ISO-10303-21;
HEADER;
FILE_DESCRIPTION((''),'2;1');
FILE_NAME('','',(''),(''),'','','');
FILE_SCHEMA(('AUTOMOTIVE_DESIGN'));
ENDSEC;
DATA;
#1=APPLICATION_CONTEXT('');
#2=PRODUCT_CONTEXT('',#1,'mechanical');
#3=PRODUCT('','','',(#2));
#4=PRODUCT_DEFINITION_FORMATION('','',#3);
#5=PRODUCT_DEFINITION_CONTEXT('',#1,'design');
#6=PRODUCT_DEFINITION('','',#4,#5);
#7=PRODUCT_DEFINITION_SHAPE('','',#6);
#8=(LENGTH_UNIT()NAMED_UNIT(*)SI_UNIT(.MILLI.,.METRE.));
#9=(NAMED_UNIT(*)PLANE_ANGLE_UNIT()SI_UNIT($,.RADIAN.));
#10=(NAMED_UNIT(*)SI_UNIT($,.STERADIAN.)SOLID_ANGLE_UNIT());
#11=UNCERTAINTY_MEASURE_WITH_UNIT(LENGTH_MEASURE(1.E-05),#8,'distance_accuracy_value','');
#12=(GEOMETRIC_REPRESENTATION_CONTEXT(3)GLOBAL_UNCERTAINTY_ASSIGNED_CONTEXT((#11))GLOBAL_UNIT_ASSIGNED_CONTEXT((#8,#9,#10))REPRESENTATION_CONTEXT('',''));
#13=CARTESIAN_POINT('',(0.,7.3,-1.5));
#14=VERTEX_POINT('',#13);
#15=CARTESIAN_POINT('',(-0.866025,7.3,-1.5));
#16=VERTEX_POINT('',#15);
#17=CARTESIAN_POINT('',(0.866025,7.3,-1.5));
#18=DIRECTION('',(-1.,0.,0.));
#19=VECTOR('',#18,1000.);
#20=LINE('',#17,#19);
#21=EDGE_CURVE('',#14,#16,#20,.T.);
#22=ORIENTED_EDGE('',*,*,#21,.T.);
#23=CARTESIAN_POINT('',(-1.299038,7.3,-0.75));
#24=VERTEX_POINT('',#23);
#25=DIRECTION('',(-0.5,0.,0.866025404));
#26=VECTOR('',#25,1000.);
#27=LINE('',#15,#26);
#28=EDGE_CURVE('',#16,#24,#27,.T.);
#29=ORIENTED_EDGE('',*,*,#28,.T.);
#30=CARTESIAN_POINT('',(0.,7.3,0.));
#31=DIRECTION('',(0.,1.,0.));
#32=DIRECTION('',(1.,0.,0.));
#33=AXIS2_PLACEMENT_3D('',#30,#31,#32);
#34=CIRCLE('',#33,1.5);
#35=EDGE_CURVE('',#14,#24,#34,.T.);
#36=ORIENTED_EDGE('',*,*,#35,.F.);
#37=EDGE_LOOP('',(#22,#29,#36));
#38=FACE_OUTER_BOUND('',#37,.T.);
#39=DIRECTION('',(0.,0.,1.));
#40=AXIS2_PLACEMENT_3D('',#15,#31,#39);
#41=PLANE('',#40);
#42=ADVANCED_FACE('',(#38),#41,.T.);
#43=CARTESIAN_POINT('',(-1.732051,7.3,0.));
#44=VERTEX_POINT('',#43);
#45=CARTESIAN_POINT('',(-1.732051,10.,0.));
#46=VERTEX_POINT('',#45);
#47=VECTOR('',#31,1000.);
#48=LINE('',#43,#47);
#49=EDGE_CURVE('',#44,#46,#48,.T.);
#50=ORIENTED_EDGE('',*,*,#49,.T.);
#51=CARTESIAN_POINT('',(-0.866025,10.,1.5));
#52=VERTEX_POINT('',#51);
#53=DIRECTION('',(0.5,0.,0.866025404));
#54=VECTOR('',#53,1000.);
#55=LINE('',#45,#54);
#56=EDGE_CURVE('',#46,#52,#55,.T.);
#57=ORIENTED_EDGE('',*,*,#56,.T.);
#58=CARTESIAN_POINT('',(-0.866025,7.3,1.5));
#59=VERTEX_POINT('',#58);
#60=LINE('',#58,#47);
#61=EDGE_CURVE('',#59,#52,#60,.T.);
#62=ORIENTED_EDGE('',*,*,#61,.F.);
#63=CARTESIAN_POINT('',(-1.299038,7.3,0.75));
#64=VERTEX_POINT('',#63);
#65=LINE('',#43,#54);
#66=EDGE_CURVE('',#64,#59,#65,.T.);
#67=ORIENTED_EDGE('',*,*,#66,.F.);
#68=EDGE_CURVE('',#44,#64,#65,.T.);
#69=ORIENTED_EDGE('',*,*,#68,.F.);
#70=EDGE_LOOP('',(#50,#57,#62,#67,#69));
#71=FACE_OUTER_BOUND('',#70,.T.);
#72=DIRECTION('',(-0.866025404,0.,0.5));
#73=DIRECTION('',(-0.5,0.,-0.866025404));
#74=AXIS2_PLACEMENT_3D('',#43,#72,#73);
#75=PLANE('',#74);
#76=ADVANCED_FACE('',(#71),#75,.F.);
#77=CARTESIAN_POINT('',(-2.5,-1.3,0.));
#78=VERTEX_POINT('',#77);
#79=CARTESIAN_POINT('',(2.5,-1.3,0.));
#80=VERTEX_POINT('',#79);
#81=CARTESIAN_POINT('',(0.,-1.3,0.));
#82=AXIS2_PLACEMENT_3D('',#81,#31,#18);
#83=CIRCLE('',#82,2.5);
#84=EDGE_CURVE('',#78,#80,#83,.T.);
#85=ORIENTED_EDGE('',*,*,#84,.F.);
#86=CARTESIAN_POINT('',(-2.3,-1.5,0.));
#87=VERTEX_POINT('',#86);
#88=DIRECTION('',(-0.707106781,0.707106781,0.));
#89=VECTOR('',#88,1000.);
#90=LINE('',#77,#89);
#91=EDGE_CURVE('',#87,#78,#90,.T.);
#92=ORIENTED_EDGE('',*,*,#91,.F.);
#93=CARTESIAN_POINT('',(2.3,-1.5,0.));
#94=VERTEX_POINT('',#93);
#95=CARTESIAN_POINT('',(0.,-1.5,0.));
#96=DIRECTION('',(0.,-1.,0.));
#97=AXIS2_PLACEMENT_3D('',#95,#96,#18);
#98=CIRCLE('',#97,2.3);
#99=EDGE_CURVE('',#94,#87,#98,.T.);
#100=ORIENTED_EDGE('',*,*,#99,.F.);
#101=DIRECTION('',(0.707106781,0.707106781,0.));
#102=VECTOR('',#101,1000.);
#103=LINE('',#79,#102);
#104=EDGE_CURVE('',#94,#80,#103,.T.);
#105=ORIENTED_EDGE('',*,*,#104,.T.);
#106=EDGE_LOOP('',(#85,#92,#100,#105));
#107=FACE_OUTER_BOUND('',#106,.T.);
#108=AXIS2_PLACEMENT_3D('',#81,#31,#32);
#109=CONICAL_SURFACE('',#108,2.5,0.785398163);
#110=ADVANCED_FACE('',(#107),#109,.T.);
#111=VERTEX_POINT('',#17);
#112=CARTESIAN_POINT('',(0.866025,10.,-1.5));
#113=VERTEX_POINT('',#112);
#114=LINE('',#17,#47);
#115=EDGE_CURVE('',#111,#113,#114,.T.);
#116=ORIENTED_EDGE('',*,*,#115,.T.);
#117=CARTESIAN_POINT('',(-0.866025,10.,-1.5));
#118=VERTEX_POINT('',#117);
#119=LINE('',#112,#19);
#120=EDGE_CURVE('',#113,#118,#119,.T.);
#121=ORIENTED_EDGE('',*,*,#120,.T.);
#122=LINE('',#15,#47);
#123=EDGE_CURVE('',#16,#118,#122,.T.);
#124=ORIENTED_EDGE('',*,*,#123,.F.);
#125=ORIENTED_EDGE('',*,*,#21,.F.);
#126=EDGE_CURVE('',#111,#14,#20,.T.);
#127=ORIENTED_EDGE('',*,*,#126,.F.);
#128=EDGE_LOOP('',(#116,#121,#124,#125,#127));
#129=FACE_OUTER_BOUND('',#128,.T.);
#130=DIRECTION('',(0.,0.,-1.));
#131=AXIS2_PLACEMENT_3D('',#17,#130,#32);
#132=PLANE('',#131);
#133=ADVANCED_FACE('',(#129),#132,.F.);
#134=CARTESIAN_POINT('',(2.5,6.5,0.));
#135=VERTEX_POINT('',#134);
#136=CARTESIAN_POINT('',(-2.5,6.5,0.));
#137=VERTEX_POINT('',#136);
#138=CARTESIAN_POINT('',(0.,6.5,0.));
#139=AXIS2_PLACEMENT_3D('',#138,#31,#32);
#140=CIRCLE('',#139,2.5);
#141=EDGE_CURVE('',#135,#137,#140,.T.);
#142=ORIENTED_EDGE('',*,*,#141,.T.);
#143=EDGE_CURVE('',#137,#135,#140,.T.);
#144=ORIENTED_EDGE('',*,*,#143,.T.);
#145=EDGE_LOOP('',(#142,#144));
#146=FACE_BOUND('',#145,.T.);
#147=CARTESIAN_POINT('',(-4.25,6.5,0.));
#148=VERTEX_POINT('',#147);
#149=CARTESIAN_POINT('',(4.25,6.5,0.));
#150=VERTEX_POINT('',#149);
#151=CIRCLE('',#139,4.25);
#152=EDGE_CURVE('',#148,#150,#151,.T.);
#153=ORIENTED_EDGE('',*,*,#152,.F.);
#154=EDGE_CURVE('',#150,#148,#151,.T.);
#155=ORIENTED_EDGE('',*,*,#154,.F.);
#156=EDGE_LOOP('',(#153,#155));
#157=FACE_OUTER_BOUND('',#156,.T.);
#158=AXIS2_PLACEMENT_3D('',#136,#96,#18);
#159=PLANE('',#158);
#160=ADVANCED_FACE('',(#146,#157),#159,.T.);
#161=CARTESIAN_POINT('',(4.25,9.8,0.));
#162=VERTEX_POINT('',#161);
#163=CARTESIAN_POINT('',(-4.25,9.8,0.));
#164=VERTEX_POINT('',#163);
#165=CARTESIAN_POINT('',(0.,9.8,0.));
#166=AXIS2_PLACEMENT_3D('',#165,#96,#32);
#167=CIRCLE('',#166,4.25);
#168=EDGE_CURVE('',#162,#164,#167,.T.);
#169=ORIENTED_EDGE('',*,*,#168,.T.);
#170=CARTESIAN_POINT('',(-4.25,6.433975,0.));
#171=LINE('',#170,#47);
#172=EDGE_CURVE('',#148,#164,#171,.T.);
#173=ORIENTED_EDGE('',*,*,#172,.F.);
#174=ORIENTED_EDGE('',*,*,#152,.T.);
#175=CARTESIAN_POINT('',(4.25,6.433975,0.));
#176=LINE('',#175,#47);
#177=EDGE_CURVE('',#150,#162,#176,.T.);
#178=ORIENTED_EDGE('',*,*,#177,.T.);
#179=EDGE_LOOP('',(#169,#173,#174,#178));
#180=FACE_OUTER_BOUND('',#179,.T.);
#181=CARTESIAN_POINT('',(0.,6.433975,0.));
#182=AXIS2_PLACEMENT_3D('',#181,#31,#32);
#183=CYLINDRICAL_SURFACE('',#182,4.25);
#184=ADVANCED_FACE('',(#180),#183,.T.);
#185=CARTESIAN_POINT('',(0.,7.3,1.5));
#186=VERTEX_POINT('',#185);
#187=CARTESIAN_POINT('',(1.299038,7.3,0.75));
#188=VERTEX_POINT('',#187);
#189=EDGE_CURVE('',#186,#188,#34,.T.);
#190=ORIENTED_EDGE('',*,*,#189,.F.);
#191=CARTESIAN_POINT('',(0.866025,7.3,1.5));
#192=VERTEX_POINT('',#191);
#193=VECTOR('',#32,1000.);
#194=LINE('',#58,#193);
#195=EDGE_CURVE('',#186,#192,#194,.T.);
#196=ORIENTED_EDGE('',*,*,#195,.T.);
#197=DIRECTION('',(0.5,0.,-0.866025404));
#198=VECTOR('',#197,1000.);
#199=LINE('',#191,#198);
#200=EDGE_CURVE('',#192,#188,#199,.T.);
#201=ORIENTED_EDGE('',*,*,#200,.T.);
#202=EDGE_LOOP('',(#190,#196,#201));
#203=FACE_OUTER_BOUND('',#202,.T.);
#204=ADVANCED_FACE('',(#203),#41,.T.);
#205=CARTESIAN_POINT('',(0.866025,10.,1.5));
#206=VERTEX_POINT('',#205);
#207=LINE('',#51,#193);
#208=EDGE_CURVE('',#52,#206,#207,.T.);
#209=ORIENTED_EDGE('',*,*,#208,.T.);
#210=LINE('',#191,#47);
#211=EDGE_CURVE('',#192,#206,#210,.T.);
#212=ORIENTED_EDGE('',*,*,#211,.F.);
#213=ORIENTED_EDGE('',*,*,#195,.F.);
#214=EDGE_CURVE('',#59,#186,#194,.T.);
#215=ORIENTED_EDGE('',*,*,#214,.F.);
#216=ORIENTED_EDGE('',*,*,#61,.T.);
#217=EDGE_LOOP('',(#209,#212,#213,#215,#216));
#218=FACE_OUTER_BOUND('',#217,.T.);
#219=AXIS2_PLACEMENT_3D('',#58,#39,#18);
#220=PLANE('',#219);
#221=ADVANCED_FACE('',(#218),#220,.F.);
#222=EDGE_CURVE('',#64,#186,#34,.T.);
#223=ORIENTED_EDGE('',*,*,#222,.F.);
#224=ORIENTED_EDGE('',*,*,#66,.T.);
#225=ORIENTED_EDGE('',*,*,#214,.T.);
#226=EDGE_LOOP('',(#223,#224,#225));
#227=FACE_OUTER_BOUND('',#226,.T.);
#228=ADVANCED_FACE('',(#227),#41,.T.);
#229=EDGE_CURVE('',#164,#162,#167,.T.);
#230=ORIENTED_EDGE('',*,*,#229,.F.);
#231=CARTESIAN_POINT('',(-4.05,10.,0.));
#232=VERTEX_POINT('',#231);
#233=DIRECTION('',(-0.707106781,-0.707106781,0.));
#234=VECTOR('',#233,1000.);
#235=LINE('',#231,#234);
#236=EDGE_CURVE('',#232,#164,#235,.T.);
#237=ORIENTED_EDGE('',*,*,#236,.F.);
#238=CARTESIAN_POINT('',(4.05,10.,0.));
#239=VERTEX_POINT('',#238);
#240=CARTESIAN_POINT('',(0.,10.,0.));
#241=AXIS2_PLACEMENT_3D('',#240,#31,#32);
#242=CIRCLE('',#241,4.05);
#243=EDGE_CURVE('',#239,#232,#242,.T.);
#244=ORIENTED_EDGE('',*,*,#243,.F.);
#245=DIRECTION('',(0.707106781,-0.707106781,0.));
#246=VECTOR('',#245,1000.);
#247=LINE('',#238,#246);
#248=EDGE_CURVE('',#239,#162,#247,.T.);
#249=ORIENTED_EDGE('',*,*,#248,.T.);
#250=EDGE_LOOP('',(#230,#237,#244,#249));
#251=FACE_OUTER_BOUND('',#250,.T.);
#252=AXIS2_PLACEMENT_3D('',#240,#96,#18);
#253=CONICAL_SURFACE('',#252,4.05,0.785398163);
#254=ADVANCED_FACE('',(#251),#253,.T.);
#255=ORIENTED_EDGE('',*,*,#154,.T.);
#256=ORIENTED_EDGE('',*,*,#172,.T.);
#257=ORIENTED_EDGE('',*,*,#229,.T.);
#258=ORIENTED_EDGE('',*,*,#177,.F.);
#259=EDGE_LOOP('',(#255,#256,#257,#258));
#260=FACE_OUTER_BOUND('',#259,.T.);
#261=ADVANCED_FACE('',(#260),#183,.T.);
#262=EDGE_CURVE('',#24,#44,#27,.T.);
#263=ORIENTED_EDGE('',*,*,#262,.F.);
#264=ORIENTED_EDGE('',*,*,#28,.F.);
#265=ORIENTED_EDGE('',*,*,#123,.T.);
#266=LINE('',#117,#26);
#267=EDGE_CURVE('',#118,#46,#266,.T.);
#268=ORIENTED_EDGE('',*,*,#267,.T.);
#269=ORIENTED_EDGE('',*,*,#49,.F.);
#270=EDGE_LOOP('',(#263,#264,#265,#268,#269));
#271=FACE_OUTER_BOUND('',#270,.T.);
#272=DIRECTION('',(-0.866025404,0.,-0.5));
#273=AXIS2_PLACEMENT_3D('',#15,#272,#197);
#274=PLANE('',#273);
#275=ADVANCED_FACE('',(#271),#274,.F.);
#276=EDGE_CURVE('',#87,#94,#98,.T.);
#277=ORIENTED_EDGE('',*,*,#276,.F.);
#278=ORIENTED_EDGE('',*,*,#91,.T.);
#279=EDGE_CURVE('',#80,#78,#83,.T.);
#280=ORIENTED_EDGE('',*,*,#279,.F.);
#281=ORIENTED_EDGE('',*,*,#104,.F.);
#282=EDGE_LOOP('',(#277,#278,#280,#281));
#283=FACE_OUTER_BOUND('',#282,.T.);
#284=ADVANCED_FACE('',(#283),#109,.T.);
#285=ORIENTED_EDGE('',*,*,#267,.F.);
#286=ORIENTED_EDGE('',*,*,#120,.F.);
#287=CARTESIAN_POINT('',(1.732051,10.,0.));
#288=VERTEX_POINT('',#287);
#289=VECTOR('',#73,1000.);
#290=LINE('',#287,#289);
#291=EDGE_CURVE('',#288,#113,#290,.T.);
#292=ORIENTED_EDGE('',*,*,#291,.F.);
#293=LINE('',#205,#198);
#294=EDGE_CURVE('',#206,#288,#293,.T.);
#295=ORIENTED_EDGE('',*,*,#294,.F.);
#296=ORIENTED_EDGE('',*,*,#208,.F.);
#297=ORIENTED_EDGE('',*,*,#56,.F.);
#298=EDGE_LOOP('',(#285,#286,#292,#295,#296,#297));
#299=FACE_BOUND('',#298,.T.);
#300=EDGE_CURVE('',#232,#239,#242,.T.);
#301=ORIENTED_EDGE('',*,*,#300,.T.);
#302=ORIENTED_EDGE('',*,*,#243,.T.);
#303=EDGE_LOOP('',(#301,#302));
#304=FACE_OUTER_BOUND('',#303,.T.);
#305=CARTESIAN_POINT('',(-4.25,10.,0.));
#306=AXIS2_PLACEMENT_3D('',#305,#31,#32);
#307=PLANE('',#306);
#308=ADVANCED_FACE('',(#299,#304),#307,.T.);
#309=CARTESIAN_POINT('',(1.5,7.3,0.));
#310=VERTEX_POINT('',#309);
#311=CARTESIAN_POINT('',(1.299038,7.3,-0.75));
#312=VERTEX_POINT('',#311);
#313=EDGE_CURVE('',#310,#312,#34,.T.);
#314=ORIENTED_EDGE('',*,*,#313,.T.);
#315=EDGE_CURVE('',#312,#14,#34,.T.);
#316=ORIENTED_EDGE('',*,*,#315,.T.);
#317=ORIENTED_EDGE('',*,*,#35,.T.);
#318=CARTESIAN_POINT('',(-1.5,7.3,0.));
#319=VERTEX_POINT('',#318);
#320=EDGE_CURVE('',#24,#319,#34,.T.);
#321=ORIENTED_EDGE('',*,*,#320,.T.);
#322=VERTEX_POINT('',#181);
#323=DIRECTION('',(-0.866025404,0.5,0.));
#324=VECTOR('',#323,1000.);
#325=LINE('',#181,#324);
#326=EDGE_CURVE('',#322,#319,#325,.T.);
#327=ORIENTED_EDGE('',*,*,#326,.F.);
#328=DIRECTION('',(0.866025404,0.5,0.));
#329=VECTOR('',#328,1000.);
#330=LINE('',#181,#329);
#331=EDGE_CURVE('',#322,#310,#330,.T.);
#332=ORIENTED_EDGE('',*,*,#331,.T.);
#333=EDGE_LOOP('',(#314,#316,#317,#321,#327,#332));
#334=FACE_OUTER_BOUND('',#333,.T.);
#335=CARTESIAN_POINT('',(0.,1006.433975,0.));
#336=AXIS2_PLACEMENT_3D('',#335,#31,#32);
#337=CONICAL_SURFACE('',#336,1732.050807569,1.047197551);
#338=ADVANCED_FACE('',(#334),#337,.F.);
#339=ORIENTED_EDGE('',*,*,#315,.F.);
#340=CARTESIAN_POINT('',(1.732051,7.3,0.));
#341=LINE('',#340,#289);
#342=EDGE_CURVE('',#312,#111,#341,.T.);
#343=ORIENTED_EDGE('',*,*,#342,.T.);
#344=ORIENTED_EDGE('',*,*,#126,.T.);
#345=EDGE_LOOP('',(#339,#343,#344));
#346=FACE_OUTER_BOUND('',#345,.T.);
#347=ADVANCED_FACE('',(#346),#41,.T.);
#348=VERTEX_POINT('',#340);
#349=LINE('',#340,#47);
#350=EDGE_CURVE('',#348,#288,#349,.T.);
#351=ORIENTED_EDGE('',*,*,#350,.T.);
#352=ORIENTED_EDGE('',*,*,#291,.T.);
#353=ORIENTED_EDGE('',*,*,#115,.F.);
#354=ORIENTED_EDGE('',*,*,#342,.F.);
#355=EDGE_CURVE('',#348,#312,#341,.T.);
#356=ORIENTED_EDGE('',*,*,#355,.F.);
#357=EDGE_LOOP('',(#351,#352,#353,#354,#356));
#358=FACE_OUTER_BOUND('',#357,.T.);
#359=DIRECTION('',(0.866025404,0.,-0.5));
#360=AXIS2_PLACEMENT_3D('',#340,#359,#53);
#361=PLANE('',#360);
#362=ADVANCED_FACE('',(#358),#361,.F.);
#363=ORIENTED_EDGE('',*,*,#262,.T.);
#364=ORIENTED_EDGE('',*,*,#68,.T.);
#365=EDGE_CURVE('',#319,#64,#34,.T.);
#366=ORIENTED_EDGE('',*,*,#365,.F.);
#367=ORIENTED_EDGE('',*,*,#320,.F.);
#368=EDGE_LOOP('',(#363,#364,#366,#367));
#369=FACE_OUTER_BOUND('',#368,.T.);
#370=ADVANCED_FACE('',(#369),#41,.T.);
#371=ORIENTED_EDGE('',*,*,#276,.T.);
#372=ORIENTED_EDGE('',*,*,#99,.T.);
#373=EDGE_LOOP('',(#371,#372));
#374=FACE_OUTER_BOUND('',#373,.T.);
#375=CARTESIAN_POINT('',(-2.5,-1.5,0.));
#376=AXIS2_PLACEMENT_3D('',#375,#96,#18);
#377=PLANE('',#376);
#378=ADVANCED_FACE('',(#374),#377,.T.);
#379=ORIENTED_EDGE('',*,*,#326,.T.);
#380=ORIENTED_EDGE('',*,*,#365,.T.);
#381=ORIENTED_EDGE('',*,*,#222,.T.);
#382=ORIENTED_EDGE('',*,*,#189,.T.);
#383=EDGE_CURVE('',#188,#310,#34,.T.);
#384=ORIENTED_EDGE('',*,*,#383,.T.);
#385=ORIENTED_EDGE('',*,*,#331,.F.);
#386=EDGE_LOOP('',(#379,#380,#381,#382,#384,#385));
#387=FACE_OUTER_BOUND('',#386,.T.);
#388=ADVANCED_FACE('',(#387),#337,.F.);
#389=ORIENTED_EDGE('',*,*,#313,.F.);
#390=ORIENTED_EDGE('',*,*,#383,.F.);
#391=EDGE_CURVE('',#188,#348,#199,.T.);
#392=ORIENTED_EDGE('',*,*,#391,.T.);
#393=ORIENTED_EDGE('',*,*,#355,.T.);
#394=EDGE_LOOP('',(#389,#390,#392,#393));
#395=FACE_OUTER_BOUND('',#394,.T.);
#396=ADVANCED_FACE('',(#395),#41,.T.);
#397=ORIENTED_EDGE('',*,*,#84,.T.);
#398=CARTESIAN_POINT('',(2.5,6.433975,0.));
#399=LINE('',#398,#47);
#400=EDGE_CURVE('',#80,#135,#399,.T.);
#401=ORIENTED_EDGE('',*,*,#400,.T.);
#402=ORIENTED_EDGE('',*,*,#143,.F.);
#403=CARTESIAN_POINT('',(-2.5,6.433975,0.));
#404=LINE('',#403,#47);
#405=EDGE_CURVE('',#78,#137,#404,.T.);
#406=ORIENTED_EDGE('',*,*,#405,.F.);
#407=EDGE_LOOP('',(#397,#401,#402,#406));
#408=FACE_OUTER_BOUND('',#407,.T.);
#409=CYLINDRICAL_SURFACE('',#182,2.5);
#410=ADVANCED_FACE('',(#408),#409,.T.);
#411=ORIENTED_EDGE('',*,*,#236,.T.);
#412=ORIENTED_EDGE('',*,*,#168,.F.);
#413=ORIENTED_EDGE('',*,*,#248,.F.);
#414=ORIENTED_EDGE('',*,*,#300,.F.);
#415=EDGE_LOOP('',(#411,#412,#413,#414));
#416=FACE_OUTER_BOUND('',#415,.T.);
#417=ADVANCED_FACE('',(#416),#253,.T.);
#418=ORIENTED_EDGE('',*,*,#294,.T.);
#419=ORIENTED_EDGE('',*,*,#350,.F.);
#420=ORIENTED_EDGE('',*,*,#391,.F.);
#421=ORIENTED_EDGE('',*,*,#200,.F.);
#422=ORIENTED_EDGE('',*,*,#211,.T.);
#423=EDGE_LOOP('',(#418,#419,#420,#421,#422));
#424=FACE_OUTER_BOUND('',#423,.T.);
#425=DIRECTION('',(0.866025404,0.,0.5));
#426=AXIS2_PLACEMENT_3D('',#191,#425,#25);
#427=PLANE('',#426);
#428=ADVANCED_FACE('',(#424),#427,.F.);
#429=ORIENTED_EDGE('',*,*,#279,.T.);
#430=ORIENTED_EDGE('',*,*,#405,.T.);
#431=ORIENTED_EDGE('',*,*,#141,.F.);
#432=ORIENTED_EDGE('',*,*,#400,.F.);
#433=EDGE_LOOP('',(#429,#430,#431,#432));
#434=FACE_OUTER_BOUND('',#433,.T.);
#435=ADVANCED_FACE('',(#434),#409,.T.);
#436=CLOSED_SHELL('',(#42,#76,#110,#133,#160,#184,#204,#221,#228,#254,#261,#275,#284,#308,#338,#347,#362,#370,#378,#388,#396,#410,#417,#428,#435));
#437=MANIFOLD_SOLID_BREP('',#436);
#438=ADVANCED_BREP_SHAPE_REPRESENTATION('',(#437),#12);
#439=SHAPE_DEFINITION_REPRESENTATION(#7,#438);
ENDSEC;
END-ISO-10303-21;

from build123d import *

# Parameters (mm, degrees)
CHAMFER1_SIZE         = 0.2
CUT_EXTRUDE1_DEPTH    = 2.7
BODY_MOVE_COPY1_ANGLE = 180


with BuildPart() as part:
    # Sketch2 → Revolve1 (revolve)
    with BuildSketch(Plane.XY):
        Polygon((1.5, -3.5), (1.5, -0.8), (0, 0.066025404), (0, 8), (2.5, 8), (2.5, 0), (4.25, 0), (4.25, -3.5), align=None)
    revolve(axis=Axis((0, 0.066025404, 0), (0, 1, 0)))

    # Chamfer1
    chamfer1_edges = [part.edges().sort_by_distance(p)[0] for p in [
        (-4.25, -3.5, 0),
        (-2.5, 8, 0),
    ]]
    chamfer(chamfer1_edges, length=CHAMFER1_SIZE)

    # Sketch3 → Cut-Extrude1 (cut)
    with BuildSketch(Plane.XZ.offset(3.5)):
        Polygon((-0.866025404, 1.5), (-1.732050808, 0), (-0.866025404, -1.5), (0.866025404, -1.5), (1.732050808, 0), (0.866025404, 1.5), align=None)
    extrude(amount=-CUT_EXTRUDE1_DEPTH, mode=Mode.SUBTRACT)


with BuildPart() as part_1:
    # Body-Move/Copy1: moved
    add(part.part.rotate(Axis((0, 3.25, 0), (1, 0, 0)), BODY_MOVE_COPY1_ANGLE))


solid = part_1.part
